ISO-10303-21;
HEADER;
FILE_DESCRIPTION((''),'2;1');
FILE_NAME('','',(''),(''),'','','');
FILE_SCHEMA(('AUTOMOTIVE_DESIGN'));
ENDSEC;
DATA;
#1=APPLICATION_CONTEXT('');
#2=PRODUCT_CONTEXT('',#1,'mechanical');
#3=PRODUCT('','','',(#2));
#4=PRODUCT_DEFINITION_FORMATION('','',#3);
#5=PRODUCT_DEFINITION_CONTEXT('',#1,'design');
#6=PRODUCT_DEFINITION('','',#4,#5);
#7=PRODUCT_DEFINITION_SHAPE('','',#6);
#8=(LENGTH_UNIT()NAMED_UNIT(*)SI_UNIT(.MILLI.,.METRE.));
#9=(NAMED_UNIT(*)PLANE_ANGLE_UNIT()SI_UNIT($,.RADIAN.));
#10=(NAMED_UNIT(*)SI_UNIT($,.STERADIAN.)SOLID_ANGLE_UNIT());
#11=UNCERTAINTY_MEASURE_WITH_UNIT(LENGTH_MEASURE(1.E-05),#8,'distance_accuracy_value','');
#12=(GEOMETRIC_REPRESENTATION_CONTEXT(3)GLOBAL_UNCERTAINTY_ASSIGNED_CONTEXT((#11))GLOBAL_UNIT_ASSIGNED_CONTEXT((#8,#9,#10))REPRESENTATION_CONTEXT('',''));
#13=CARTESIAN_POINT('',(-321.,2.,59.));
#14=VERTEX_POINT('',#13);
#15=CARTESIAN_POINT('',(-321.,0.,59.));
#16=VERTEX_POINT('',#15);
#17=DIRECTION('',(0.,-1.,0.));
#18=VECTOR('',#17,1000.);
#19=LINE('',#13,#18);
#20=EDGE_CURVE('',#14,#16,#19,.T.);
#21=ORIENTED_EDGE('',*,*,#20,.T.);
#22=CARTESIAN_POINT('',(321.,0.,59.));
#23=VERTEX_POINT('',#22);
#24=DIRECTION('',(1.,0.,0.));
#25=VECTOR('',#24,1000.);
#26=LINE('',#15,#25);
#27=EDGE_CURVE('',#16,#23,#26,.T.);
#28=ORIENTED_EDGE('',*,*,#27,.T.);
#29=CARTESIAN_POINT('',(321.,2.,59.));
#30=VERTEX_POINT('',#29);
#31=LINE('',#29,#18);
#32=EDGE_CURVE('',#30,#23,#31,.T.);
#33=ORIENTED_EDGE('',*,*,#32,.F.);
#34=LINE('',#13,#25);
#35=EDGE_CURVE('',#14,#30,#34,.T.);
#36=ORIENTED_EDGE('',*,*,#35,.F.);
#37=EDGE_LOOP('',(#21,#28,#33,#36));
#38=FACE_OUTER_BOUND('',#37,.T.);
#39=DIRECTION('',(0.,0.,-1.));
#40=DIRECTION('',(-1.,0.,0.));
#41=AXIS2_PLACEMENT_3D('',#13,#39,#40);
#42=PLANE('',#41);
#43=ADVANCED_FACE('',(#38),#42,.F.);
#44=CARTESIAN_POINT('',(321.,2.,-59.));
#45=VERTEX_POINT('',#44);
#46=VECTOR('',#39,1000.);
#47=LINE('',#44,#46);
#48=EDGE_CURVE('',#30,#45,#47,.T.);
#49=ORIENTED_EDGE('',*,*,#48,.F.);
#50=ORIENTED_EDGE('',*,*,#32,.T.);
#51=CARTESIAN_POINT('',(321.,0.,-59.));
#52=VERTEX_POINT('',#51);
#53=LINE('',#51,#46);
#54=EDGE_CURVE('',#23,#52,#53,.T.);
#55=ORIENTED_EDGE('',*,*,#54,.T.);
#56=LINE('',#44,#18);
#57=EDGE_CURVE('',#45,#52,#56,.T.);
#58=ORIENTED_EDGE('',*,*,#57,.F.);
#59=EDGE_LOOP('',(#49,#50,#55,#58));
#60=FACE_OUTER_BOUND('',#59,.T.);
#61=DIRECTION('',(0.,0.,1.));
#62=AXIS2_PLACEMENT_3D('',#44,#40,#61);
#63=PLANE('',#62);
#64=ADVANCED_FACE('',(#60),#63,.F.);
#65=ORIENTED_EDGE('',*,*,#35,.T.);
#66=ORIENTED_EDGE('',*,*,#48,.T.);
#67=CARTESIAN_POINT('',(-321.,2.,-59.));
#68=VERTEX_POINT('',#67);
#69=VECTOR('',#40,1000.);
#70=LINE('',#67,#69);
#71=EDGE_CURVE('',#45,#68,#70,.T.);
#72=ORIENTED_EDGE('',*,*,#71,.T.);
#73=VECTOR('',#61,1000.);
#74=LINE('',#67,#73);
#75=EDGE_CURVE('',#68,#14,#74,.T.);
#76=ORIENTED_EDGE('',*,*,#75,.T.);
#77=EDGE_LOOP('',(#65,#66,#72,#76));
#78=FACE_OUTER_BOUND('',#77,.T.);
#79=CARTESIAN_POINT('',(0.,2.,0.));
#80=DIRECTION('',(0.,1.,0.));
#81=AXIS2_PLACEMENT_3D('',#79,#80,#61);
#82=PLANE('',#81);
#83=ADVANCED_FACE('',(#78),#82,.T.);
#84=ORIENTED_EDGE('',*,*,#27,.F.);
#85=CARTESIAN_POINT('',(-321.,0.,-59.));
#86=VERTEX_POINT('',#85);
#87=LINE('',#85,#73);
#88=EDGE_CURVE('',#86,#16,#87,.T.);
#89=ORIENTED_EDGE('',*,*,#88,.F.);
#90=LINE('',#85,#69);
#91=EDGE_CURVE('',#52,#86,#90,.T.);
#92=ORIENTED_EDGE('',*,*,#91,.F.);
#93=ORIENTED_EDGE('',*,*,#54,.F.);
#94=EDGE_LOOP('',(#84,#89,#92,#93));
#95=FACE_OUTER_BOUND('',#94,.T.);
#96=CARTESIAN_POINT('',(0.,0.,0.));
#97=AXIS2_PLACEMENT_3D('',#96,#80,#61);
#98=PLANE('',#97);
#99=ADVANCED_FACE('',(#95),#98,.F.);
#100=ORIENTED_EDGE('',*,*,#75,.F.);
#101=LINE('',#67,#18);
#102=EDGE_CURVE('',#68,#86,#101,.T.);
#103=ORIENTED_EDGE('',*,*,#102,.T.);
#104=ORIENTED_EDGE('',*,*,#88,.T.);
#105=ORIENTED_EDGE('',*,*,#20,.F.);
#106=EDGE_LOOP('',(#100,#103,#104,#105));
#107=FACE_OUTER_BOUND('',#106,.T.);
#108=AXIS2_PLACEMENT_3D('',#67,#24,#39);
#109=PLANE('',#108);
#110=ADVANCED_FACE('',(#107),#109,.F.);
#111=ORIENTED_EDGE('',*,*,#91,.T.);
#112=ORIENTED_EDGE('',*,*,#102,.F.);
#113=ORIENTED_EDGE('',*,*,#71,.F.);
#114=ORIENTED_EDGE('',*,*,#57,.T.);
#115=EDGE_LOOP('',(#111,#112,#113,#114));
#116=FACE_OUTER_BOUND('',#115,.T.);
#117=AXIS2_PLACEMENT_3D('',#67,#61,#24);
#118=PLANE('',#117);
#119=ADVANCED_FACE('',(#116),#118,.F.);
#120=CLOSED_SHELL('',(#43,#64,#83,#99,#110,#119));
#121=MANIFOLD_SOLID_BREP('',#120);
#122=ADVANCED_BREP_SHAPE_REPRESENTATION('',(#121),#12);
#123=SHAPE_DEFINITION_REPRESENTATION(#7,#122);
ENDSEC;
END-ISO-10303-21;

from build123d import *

# Parameters (mm, degrees)
SKETCH1_W           = 642
SKETCH1_H           = 118
BOSS_EXTRUDE1_DEPTH = 2


with BuildPart() as part:
    # Sketch1 → Boss-Extrude1 (new body)
    with BuildSketch(Plane(origin=(0, 0, 0), x_dir=(1, 0, 0), z_dir=(0, 1, 0))):
        Rectangle(SKETCH1_W, SKETCH1_H)
    extrude(amount=BOSS_EXTRUDE1_DEPTH)


solid = part.part
